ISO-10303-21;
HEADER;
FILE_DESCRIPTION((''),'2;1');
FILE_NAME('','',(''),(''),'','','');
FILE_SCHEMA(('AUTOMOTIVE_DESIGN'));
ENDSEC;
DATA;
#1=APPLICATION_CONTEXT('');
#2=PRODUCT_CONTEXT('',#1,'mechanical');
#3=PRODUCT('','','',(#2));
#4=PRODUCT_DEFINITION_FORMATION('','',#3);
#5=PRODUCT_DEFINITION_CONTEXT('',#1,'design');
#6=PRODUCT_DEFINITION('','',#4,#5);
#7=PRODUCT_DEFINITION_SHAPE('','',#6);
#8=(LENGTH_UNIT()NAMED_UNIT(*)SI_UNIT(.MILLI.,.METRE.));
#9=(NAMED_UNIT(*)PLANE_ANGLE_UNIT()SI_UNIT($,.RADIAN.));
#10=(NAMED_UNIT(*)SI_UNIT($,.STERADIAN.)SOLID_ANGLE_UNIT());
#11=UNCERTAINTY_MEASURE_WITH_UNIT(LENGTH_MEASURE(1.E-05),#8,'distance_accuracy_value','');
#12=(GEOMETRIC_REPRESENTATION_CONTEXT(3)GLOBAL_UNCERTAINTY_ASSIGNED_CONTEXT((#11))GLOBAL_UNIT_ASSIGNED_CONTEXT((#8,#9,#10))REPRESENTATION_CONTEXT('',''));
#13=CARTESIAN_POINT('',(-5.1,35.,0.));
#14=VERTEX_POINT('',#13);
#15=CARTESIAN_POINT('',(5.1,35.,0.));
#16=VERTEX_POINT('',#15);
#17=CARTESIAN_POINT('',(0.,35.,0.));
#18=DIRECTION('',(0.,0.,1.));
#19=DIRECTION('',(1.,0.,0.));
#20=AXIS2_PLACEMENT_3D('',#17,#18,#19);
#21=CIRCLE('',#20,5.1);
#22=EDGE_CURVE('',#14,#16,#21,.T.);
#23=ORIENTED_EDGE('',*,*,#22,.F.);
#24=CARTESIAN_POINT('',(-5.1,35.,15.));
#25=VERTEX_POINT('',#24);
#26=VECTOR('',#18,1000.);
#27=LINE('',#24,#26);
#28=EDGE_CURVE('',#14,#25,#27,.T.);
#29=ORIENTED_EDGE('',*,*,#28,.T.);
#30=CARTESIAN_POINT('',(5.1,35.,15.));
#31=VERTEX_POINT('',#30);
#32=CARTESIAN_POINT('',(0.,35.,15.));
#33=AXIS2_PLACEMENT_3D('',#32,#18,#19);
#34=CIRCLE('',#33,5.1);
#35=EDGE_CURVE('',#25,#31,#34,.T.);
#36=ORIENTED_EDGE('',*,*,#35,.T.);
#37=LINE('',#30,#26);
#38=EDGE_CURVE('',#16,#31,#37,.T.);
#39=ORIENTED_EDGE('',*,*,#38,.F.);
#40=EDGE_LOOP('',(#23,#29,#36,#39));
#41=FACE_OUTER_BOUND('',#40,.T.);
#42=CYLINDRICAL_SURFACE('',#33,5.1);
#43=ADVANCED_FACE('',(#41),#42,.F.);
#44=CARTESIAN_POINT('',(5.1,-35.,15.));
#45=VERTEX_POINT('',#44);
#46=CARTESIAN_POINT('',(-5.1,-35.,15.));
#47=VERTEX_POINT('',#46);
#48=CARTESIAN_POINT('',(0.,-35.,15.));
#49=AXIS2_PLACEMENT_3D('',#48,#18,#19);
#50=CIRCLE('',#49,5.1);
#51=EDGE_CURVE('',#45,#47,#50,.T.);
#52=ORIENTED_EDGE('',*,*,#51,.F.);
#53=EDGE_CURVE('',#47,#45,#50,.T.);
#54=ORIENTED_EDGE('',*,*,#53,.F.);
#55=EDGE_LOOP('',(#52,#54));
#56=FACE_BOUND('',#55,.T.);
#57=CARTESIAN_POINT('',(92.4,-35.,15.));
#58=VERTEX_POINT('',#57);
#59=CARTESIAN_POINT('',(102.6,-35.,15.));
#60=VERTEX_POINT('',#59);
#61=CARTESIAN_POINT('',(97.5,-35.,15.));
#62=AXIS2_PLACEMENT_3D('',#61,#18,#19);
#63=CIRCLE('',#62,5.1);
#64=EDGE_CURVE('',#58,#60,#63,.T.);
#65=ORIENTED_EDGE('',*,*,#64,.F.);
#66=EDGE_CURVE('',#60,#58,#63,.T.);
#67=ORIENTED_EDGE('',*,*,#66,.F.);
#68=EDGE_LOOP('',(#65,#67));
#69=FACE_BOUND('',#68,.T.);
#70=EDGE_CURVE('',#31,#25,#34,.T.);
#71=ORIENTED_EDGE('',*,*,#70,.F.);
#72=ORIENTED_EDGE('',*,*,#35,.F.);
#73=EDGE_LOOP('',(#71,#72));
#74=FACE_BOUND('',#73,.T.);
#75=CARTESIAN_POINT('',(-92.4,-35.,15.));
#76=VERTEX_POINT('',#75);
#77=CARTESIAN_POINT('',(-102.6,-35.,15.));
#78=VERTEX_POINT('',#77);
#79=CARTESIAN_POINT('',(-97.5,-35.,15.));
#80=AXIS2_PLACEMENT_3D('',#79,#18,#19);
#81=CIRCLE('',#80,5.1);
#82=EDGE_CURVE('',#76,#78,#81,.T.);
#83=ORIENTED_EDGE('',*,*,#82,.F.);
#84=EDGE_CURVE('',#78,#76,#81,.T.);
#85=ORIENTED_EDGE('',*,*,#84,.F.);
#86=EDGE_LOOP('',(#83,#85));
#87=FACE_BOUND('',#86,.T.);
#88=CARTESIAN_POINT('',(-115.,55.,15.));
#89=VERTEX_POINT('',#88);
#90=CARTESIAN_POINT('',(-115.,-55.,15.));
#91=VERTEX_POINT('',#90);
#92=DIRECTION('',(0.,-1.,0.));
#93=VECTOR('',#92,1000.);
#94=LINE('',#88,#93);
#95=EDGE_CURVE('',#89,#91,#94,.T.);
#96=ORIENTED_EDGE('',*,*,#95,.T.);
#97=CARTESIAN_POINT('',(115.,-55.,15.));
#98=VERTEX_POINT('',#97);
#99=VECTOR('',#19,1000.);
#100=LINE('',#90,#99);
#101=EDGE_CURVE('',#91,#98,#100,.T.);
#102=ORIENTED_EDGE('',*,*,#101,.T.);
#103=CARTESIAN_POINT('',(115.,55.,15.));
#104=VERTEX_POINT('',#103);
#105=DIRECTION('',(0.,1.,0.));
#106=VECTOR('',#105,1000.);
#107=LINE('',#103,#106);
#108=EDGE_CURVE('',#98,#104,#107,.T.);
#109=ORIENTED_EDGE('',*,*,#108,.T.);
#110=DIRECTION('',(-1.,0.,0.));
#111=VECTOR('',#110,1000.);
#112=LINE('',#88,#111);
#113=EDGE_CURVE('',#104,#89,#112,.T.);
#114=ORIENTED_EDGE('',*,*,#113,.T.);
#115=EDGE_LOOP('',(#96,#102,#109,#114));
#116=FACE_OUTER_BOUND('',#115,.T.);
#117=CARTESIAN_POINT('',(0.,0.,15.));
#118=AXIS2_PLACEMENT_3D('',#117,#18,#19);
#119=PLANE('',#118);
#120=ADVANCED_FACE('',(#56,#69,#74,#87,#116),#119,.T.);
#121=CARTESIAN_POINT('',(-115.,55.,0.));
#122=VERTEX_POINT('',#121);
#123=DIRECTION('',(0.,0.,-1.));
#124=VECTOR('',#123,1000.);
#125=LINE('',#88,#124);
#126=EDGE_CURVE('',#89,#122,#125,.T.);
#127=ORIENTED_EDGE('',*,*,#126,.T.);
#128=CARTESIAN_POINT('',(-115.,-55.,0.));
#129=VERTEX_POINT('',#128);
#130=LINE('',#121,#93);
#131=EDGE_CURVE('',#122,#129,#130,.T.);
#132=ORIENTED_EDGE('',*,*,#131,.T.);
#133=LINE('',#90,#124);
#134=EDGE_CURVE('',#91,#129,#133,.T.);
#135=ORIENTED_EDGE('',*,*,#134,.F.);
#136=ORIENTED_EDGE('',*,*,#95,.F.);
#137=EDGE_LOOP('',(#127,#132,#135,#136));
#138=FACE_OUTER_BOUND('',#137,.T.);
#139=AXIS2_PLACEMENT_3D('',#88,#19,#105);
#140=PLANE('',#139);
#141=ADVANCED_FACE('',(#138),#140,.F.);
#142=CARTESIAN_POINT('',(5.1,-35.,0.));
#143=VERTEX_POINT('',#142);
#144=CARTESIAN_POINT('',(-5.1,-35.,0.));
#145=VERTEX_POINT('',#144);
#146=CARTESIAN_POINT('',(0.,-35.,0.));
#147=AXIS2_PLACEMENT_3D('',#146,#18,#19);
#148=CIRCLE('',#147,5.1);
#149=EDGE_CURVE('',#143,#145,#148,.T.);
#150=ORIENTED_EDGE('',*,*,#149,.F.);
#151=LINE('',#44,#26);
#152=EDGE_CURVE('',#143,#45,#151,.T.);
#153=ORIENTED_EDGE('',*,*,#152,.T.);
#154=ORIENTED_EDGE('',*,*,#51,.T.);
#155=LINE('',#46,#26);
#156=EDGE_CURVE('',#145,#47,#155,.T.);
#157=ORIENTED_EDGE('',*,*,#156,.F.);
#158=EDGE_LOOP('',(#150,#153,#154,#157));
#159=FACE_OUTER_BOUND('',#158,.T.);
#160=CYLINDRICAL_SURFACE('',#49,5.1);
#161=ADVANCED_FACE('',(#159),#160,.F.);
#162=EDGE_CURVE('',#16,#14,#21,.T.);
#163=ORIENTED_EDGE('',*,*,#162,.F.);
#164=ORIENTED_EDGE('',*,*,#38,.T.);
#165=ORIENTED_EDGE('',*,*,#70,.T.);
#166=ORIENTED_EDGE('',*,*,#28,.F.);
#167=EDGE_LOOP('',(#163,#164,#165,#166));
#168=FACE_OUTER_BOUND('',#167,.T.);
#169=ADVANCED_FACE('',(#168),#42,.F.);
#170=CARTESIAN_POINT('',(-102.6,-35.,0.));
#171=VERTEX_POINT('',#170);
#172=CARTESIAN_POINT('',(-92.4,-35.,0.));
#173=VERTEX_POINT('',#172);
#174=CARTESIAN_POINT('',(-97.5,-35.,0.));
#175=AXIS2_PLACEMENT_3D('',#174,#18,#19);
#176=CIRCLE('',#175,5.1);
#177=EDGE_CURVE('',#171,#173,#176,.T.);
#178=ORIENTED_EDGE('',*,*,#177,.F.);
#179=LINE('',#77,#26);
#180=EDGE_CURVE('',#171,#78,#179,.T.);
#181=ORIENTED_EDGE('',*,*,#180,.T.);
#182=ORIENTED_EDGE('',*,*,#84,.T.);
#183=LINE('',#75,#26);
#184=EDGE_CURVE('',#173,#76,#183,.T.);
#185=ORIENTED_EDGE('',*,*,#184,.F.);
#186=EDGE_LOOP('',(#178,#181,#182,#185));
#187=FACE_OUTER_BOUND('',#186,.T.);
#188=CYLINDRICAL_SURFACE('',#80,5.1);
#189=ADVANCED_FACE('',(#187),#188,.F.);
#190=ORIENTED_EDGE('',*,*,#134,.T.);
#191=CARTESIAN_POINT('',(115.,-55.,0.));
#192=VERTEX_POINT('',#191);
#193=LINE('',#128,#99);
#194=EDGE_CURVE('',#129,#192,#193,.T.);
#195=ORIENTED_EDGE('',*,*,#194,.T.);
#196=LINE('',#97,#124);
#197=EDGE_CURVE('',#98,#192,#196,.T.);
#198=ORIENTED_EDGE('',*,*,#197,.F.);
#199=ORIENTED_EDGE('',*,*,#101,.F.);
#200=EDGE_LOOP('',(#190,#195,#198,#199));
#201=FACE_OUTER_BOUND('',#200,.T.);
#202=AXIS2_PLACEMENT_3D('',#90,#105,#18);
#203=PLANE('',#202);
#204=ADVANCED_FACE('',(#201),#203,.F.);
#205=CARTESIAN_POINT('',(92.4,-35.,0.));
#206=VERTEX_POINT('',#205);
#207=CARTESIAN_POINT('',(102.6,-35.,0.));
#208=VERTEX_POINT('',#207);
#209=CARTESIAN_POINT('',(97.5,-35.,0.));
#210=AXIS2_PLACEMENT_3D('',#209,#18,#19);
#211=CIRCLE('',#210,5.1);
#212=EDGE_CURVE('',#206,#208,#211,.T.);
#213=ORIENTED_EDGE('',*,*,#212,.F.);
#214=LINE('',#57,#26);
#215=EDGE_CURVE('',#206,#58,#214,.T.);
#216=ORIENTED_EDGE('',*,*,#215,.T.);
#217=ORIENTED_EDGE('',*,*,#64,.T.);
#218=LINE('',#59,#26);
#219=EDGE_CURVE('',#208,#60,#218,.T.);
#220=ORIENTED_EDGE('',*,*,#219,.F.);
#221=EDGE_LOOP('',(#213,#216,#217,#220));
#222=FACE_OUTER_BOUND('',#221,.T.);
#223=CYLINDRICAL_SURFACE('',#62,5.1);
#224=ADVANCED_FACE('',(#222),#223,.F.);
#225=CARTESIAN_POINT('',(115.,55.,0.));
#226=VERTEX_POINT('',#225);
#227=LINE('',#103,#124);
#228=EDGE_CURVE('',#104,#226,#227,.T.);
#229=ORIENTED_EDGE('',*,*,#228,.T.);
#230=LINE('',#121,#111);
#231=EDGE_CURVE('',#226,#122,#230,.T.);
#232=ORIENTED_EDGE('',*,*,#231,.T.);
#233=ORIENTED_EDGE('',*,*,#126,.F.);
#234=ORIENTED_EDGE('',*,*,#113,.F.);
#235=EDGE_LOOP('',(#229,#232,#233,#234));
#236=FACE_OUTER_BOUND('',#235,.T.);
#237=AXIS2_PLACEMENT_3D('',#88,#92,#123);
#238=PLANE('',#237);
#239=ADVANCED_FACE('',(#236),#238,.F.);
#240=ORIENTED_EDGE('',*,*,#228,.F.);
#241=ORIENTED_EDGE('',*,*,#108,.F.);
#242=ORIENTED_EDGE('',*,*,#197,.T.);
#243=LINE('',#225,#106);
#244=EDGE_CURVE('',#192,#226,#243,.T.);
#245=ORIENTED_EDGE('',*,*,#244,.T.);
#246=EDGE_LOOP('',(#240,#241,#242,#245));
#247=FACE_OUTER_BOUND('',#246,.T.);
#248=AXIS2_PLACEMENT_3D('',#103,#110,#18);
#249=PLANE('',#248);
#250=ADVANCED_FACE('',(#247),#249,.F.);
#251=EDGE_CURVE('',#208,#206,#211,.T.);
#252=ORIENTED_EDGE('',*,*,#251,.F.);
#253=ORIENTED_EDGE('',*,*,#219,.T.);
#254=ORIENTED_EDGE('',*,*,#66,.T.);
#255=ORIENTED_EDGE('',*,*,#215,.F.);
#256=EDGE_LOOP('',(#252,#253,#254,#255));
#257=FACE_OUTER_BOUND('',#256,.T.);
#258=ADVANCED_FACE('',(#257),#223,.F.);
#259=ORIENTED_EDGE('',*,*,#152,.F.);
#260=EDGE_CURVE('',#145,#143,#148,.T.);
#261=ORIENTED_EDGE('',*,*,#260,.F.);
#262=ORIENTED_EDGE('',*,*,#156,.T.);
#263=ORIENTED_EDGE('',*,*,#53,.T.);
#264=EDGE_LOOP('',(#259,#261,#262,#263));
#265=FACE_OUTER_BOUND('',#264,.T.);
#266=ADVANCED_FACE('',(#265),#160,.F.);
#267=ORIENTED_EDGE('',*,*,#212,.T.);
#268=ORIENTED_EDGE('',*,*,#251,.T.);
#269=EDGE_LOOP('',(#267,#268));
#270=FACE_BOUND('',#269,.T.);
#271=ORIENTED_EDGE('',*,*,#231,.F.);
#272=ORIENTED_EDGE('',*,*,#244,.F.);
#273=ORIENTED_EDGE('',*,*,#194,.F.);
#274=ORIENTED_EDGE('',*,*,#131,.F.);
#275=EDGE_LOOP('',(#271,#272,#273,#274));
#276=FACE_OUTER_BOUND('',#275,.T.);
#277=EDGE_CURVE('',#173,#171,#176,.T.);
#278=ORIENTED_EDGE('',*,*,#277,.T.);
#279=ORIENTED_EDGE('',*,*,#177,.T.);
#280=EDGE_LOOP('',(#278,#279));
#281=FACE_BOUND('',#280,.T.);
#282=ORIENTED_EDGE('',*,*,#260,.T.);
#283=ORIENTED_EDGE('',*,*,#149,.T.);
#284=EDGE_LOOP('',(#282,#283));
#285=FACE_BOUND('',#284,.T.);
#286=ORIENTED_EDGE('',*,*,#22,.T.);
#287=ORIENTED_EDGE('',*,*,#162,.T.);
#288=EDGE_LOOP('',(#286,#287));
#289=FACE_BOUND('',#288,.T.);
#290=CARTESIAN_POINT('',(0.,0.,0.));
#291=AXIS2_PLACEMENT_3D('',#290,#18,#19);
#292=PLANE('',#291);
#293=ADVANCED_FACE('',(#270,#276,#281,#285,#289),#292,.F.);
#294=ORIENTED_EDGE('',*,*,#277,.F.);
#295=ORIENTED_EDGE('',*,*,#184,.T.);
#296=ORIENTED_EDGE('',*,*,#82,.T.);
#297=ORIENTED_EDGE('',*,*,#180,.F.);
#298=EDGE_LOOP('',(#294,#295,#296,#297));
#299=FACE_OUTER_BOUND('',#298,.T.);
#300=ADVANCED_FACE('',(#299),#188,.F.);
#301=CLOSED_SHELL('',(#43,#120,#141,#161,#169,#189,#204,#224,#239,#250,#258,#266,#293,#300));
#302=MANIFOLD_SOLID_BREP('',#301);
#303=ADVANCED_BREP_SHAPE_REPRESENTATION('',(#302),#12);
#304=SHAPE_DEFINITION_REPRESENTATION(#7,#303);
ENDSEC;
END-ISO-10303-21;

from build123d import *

# Parameters (mm, degrees)
SKETCH1_W              = 230
SKETCH1_H              = 110
BOSS_EXTRUDE1_DEPTH    = 15
M12_TAPPED_HOLE2_D     = 10.2
M12_TAPPED_HOLE2_DEPTH = 29.25
M12_TAPPED_HOLE2_TIP   = 3.064389157


with BuildPart() as part:
    # Sketch1 → Boss-Extrude1 (new body)
    with BuildSketch(Plane.XY):
        Rectangle(SKETCH1_W, SKETCH1_H)
    extrude(amount=BOSS_EXTRUDE1_DEPTH)

    # M12 Tapped Hole2
    with Locations(Plane.XY.offset(15)):
        with Locations((-97.5, -35), (97.5, -35), (0, 35), (0, -35)):
            Hole(M12_TAPPED_HOLE2_D / 2, depth=M12_TAPPED_HOLE2_DEPTH)
            with Locations((0, 0, -(M12_TAPPED_HOLE2_DEPTH + M12_TAPPED_HOLE2_TIP / 2))):  # 118° drill point
                Cone(0, M12_TAPPED_HOLE2_D / 2, M12_TAPPED_HOLE2_TIP, mode=Mode.SUBTRACT)


solid = part.part
